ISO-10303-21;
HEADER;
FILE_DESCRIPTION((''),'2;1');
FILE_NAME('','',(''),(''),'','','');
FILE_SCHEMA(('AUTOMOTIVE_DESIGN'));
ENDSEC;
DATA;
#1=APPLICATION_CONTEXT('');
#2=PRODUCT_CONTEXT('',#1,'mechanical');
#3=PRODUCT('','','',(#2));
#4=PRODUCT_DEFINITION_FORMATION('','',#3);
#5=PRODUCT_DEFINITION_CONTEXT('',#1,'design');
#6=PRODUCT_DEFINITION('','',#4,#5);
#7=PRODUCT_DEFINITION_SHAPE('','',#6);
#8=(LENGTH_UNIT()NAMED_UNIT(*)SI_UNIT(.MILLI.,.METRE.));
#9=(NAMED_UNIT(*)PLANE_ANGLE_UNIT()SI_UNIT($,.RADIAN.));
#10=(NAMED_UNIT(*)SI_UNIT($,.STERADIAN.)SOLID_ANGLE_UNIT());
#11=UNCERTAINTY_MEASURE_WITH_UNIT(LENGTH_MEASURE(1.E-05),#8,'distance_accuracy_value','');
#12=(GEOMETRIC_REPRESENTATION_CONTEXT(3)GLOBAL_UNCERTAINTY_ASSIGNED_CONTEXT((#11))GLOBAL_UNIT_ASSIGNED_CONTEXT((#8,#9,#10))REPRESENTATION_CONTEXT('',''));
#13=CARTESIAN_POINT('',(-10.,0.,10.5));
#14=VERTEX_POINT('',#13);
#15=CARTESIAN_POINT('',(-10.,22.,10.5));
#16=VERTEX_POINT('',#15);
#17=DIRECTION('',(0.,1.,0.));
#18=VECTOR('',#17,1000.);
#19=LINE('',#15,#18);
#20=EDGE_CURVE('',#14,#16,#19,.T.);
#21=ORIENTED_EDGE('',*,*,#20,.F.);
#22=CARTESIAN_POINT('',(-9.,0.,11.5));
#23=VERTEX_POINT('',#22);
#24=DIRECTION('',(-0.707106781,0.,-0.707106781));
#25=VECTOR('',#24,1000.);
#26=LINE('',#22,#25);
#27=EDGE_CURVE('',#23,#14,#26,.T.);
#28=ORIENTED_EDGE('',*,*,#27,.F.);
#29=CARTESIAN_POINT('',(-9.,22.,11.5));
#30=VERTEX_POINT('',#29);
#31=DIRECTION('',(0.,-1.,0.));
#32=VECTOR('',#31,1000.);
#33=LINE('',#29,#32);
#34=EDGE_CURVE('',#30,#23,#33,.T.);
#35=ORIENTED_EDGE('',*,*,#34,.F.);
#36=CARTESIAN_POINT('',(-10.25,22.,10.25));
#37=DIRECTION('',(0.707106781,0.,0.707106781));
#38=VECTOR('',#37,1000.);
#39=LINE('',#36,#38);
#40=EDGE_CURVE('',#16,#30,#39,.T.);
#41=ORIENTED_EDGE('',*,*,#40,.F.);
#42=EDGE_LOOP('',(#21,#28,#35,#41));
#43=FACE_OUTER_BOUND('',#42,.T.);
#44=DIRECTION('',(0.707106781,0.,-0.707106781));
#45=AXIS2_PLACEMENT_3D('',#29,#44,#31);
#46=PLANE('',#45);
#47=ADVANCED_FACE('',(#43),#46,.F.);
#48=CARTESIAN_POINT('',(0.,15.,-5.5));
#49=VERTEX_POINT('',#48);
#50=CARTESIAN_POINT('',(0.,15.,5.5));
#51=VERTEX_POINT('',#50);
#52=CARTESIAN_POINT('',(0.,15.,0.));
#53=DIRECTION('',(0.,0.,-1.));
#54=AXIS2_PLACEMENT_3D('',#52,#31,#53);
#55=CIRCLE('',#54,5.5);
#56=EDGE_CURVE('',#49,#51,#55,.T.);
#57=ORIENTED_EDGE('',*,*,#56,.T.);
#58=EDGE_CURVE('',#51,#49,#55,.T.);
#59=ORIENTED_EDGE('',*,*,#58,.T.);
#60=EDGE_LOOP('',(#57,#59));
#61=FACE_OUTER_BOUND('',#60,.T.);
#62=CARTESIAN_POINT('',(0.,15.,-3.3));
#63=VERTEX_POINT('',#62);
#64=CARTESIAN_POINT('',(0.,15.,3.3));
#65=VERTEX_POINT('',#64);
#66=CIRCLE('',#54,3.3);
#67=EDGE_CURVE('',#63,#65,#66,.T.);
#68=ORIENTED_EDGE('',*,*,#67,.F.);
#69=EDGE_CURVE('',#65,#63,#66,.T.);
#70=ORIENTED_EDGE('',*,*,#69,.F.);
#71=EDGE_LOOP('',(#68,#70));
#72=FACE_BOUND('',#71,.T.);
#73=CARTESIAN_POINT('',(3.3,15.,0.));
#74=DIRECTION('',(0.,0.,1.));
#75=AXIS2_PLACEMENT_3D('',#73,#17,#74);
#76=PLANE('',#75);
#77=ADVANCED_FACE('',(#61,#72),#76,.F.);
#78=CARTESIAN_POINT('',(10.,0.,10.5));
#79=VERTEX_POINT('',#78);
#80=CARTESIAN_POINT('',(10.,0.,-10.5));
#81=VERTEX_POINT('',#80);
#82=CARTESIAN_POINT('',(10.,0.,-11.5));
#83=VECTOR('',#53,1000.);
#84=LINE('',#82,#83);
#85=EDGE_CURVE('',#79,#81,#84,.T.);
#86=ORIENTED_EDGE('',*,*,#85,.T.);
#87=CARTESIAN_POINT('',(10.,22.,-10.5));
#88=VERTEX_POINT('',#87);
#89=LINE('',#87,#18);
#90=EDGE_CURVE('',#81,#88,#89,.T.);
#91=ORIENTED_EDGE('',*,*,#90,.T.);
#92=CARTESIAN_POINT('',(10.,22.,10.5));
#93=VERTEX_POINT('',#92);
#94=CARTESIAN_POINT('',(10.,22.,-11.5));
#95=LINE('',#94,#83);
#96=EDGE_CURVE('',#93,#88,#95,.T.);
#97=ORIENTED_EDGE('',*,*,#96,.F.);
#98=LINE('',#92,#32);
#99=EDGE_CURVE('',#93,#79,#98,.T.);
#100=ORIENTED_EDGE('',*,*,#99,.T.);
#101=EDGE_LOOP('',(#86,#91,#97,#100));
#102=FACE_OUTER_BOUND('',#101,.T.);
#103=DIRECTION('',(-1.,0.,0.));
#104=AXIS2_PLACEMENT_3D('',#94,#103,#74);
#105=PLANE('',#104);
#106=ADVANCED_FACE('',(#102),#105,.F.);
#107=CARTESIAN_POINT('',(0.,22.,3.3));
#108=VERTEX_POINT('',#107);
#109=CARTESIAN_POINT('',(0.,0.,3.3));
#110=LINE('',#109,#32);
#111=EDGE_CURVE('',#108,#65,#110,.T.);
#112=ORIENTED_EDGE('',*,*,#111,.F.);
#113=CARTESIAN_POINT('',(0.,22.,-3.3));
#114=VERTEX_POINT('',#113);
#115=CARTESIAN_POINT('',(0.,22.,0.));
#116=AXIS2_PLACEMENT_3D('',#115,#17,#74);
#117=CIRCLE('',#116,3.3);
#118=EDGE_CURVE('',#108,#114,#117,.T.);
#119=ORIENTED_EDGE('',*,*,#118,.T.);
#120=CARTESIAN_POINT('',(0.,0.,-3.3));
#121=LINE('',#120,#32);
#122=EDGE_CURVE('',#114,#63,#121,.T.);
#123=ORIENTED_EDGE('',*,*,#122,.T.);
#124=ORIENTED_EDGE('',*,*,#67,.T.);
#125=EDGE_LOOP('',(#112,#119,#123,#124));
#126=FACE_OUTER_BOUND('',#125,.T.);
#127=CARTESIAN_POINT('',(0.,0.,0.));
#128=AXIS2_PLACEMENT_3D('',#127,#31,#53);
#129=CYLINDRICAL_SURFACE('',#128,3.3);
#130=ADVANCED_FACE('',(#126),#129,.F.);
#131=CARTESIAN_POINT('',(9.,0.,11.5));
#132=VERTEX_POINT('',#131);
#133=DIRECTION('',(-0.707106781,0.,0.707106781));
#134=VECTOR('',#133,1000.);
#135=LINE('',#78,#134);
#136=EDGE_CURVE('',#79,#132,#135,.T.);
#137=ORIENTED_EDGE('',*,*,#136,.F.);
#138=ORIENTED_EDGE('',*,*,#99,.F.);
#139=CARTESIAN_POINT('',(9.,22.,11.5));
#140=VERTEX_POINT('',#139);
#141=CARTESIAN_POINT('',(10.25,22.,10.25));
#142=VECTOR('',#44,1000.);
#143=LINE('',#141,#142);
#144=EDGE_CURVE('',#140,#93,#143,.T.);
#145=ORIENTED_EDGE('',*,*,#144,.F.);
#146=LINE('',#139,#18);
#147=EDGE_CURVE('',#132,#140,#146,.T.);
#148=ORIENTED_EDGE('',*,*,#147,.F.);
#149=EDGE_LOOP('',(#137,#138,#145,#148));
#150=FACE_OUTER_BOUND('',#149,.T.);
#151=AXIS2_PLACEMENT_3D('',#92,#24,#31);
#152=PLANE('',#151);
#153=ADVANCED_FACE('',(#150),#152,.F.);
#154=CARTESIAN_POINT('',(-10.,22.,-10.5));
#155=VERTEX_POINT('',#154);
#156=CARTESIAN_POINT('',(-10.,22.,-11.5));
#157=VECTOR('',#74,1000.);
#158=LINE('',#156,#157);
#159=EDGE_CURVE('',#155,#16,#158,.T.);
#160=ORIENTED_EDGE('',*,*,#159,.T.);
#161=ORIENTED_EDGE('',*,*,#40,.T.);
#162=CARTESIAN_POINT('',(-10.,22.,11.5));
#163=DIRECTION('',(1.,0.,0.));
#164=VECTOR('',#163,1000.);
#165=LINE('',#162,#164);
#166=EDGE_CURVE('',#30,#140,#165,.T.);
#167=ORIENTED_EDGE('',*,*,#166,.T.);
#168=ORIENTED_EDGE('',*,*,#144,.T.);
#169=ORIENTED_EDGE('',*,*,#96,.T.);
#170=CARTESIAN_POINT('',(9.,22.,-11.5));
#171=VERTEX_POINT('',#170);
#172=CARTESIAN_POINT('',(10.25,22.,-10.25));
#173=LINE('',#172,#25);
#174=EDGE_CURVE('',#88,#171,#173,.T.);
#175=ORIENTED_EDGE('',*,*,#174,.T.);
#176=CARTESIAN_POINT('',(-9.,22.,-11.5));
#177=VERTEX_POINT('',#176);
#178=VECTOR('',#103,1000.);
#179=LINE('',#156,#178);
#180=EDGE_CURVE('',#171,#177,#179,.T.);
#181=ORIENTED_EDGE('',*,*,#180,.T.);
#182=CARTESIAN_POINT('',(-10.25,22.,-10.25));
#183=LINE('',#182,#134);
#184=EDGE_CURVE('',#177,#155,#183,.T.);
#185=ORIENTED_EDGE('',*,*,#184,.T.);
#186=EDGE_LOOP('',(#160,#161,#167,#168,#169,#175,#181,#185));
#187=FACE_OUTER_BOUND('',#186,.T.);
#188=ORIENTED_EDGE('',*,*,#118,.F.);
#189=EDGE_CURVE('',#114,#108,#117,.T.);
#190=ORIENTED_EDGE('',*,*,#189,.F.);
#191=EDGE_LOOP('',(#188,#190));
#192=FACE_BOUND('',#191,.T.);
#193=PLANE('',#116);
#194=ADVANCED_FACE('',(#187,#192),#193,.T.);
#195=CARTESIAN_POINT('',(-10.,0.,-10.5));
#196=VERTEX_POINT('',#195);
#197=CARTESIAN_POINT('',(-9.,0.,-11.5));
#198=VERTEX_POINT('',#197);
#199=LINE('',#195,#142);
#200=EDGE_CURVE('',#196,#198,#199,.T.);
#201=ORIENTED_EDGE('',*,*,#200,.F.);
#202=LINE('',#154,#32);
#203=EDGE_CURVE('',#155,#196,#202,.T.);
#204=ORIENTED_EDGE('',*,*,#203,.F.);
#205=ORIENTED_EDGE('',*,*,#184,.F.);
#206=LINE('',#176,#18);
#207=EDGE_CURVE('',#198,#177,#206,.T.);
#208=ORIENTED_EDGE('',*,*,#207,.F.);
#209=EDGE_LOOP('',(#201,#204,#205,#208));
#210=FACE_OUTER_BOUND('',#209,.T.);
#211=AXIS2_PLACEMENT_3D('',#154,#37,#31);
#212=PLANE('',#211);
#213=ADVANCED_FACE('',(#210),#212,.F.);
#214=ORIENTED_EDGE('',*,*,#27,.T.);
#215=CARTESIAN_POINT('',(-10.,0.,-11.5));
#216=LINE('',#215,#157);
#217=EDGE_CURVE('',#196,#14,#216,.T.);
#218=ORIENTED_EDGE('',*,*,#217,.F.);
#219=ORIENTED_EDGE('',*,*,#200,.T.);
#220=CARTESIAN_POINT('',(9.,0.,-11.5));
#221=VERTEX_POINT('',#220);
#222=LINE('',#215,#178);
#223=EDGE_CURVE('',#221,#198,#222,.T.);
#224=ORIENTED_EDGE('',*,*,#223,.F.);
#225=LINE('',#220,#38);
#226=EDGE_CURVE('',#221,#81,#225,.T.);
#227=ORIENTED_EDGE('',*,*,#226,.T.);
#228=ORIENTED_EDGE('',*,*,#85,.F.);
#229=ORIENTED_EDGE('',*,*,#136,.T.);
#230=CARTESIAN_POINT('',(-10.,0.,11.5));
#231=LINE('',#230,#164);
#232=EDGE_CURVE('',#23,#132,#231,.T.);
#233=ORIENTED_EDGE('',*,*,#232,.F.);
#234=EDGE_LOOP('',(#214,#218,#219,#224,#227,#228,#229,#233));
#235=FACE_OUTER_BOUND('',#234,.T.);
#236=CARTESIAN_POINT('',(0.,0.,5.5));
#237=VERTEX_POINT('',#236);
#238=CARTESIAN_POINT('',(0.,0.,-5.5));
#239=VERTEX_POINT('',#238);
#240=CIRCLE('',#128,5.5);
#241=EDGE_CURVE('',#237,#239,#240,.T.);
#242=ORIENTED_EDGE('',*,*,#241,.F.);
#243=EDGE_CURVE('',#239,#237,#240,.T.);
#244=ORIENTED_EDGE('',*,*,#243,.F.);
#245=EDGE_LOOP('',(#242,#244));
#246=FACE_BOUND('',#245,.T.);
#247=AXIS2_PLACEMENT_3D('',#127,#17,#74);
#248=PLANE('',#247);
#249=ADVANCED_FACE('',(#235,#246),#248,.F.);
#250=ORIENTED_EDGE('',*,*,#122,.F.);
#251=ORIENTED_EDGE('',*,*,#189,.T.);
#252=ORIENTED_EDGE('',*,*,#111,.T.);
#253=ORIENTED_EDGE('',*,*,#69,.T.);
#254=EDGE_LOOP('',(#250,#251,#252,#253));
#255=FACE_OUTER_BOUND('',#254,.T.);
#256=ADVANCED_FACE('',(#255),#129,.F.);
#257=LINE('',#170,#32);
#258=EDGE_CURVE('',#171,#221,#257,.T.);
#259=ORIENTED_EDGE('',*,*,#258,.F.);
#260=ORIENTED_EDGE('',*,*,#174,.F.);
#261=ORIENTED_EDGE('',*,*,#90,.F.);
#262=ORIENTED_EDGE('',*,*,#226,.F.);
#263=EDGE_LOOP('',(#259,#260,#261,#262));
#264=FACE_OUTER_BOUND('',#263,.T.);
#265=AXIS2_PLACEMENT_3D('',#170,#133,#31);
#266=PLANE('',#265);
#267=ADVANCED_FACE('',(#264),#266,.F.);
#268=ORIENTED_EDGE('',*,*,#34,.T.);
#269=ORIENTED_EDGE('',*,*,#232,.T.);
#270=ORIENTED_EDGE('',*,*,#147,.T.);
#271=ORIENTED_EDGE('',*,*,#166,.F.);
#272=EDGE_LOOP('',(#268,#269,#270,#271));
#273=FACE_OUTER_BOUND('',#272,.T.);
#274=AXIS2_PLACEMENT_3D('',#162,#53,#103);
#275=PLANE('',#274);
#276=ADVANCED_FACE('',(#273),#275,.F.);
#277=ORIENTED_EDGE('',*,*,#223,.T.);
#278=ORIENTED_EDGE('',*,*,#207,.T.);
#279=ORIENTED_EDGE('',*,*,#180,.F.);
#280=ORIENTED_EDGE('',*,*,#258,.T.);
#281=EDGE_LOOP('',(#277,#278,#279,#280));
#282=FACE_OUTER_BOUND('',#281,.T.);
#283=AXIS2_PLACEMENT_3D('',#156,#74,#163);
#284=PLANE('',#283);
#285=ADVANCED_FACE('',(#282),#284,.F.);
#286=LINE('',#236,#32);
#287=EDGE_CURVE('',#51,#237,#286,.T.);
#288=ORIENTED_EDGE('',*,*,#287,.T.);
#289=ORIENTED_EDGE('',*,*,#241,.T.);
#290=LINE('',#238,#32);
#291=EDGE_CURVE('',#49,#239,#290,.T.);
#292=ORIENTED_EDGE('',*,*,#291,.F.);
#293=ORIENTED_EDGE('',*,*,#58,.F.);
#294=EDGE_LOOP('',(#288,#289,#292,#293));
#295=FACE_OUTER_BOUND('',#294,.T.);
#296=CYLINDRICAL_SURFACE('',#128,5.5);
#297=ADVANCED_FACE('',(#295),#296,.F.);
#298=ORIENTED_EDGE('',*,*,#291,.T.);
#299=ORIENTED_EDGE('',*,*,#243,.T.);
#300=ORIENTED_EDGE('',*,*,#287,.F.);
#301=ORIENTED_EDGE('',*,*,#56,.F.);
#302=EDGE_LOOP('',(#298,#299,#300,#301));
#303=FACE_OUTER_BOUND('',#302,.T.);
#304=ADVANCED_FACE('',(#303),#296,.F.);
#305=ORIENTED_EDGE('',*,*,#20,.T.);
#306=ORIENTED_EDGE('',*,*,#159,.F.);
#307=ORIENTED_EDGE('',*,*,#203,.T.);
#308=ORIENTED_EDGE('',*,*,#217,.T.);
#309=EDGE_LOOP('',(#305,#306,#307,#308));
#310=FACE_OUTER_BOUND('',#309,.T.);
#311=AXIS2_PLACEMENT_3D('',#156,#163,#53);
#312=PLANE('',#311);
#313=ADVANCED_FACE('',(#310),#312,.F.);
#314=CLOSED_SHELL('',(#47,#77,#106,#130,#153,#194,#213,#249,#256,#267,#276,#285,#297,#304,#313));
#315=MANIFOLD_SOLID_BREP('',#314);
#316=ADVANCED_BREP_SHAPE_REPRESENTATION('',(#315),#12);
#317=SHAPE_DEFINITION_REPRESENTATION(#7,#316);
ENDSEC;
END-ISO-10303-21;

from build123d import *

# Parameters (mm, degrees)
SKETCH_1_W                   = 20
SKETCH_1_H                   = 23
EXTRUDE_1_DEPTH              = 22
HOLE_WIZARD_M6_1_D           = 6.6
HOLE_WIZARD_M6_1_DEPTH       = 22.25
HOLE_WIZARD_M6_1_CBORE_D     = 11
HOLE_WIZARD_M6_1_CBORE_DEPTH = 15
HOLE_WIZARD_M6_1_TIP         = 1.982840043
CHAMFER_1_SIZE               = 1


with BuildPart() as part:
    # 草图1 → 凸台-拉伸1 (new body)
    with BuildSketch(Plane(origin=(0, 0, 0), x_dir=(1, 0, 0), z_dir=(0, 1, 0))):
        Rectangle(SKETCH_1_W, SKETCH_1_H)
    extrude(amount=EXTRUDE_1_DEPTH)

    # M6 六角凹头螺钉的柱形沉头孔1
    with Locations(Plane(origin=(0, 0, 0), x_dir=(-1, 0, 0), z_dir=(0, -1, 0))):
        with Locations((0, 0)):
            CounterBoreHole(HOLE_WIZARD_M6_1_D / 2, HOLE_WIZARD_M6_1_CBORE_D / 2, HOLE_WIZARD_M6_1_CBORE_DEPTH, depth=HOLE_WIZARD_M6_1_DEPTH)
            with Locations((0, 0, -(HOLE_WIZARD_M6_1_DEPTH + HOLE_WIZARD_M6_1_TIP / 2))):  # 118° drill point
                Cone(0, HOLE_WIZARD_M6_1_D / 2, HOLE_WIZARD_M6_1_TIP, mode=Mode.SUBTRACT)

    # 倒角1
    chamfer_1_edges = [part.edges().sort_by_distance(p)[0] for p in [
        (10, 11, 11.5),
        (-10, 11, 11.5),
        (-10, 11, -11.5),
        (10, 11, -11.5),
    ]]
    chamfer(chamfer_1_edges, length=CHAMFER_1_SIZE)


solid = part.part
